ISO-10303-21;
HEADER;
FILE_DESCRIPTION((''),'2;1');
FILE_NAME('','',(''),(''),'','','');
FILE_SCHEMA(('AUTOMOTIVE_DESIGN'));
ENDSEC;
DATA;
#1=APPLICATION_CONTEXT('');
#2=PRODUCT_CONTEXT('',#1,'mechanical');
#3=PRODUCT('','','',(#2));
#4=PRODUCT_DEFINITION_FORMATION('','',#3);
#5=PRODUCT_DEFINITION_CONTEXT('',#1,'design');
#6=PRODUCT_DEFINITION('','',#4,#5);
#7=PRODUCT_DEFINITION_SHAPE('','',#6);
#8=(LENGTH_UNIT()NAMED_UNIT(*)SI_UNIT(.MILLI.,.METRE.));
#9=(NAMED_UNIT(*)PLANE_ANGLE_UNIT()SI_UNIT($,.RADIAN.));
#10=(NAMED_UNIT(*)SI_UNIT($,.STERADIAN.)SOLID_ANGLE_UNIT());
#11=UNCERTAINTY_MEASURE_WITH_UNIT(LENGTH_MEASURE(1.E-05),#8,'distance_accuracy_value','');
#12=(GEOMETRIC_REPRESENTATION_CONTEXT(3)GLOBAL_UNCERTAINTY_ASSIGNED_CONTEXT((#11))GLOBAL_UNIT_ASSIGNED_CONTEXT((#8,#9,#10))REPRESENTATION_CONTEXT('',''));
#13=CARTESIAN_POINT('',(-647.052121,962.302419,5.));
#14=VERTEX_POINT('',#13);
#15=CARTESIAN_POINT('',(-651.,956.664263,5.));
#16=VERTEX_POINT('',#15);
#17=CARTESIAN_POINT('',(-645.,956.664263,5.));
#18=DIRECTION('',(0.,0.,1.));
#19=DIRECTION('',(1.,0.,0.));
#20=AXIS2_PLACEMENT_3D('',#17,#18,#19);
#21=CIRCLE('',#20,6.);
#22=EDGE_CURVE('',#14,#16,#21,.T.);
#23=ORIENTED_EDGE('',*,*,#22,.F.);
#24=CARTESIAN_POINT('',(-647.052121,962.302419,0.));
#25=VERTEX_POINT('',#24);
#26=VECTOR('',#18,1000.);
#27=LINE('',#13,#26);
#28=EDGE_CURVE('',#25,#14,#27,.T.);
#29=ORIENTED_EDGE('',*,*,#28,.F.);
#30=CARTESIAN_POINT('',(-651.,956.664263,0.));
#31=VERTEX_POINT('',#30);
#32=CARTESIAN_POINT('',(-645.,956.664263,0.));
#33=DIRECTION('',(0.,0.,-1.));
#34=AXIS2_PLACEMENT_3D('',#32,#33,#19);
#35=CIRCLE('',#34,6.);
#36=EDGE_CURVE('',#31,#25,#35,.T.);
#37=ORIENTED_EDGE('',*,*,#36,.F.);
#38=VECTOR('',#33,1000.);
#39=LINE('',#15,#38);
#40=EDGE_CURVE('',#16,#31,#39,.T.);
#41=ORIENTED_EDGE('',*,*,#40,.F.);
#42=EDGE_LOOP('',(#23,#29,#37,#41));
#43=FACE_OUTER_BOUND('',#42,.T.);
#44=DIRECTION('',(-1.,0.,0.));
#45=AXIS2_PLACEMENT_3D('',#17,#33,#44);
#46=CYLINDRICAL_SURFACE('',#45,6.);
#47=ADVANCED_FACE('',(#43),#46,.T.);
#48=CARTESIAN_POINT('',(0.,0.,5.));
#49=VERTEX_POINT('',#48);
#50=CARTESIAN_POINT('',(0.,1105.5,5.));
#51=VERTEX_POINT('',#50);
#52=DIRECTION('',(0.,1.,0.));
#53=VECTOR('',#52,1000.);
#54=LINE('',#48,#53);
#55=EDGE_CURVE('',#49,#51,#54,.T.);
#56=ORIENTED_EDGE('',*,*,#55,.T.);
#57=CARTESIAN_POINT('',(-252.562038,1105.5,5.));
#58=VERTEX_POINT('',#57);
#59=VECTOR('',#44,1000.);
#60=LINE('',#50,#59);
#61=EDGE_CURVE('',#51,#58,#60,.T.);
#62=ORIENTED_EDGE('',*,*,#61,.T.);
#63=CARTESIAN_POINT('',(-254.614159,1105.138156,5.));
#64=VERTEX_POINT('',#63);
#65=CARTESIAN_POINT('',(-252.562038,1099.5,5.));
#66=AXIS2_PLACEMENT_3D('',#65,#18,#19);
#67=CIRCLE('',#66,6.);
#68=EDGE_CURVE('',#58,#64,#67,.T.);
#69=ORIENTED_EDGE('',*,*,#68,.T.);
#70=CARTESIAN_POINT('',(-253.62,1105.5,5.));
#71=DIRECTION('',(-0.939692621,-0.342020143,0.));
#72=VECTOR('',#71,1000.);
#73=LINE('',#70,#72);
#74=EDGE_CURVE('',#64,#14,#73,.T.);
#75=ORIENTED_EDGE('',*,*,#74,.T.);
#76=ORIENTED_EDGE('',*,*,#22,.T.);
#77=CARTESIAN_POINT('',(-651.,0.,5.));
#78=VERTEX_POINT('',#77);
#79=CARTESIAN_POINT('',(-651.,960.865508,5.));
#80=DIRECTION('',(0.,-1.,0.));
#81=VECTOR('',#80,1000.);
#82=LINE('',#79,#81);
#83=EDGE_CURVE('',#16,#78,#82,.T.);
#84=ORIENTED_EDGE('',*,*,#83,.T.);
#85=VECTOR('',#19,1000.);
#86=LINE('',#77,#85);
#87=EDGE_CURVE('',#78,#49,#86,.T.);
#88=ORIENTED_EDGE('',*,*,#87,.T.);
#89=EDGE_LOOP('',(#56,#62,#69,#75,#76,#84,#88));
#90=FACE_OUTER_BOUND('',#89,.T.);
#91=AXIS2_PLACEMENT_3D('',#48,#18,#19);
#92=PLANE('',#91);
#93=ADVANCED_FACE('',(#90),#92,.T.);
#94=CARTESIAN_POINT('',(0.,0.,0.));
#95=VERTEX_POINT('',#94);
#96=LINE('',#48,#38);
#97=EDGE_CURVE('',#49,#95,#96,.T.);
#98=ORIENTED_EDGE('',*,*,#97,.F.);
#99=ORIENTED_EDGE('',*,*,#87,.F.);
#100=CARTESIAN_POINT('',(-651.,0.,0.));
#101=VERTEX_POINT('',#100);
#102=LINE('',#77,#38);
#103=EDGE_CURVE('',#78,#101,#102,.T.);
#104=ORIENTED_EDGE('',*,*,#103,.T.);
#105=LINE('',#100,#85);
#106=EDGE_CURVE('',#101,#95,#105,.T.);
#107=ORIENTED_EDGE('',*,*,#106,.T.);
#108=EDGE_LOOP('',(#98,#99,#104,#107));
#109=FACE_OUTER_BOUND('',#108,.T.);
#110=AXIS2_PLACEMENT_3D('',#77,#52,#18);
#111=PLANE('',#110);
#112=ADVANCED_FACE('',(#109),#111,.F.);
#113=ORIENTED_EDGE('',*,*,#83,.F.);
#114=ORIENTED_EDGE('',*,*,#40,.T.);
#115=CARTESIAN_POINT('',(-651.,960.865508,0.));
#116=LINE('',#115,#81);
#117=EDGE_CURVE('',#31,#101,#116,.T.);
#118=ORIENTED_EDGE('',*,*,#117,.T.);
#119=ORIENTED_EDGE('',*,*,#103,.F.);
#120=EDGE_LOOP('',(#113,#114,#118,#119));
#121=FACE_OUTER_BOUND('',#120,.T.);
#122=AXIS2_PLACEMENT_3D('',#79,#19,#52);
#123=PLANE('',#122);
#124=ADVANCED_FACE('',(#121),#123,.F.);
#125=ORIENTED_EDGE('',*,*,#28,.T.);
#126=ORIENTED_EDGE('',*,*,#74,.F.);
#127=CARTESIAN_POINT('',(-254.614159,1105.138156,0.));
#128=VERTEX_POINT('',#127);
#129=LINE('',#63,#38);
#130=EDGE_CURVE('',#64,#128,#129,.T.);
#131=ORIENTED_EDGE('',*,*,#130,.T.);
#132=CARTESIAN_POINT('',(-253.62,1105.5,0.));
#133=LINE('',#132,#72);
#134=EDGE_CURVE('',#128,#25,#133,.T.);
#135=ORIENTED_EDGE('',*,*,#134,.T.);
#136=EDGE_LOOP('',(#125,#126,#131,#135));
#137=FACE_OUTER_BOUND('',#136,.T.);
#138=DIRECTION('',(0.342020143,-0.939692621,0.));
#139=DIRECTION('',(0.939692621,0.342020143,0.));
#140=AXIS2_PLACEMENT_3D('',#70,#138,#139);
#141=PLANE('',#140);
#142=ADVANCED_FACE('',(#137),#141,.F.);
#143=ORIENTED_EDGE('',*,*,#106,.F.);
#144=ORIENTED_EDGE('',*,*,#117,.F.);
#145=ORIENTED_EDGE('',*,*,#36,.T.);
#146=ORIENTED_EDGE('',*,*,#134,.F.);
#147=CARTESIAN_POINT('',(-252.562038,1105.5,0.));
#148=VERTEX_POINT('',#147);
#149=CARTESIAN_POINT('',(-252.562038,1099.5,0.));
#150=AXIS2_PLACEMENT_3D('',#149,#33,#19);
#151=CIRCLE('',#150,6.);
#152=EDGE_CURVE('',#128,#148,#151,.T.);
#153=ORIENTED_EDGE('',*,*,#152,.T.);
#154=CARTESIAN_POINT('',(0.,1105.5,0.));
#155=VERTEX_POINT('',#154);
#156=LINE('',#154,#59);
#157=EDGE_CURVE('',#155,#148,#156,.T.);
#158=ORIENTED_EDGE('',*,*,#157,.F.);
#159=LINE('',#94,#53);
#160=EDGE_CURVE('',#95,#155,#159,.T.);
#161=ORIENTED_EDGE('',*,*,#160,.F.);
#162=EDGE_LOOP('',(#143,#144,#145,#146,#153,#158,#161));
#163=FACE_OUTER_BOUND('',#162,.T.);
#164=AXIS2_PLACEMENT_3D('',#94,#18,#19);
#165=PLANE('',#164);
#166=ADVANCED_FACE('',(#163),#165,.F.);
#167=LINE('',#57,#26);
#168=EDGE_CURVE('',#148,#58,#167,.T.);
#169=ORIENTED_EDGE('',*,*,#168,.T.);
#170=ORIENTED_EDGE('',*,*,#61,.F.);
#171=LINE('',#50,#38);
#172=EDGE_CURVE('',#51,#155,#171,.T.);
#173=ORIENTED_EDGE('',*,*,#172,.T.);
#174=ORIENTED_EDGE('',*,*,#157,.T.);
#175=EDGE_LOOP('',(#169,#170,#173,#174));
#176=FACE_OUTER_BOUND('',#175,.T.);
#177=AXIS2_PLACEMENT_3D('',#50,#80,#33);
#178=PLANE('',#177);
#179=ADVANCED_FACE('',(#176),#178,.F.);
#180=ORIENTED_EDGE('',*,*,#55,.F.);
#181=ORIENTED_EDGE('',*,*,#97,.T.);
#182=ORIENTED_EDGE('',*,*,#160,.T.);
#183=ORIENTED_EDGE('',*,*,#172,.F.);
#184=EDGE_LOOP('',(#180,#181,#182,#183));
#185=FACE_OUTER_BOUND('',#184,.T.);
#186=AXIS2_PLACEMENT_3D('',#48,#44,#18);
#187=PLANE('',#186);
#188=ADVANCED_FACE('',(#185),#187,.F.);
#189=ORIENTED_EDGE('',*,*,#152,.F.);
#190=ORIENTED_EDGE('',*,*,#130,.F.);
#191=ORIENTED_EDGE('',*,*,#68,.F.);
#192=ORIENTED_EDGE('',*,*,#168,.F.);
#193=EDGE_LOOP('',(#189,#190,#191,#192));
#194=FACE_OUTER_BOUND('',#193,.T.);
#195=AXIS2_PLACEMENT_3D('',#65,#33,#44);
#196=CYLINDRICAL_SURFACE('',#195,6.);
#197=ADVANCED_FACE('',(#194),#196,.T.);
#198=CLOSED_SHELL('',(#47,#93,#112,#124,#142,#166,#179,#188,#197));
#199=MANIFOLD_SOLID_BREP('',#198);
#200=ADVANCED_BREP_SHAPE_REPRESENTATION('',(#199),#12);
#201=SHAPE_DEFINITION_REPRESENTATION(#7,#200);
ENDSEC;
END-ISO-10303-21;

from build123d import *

# Parameters (mm, degrees)
BOSS_EXTRUDE1_DEPTH = 5
FILLET1_R           = 6


with BuildPart() as part:
    # Sketch1 → Boss-Extrude1 (new body)
    with BuildSketch(Plane.XY):
        Polygon((0, 0), (0, 1105.5), (-253.62, 1105.5), (-651, 960.865508307), (-651, 0), align=None)
    extrude(amount=BOSS_EXTRUDE1_DEPTH)

    # Fillet1
    fillet1_edges = [part.edges().sort_by_distance(p)[0] for p in [
        (-651, 960.865508307, 2.5),
        (-253.62, 1105.5, 2.5),
    ]]
    fillet(fillet1_edges, radius=FILLET1_R)


solid = part.part
